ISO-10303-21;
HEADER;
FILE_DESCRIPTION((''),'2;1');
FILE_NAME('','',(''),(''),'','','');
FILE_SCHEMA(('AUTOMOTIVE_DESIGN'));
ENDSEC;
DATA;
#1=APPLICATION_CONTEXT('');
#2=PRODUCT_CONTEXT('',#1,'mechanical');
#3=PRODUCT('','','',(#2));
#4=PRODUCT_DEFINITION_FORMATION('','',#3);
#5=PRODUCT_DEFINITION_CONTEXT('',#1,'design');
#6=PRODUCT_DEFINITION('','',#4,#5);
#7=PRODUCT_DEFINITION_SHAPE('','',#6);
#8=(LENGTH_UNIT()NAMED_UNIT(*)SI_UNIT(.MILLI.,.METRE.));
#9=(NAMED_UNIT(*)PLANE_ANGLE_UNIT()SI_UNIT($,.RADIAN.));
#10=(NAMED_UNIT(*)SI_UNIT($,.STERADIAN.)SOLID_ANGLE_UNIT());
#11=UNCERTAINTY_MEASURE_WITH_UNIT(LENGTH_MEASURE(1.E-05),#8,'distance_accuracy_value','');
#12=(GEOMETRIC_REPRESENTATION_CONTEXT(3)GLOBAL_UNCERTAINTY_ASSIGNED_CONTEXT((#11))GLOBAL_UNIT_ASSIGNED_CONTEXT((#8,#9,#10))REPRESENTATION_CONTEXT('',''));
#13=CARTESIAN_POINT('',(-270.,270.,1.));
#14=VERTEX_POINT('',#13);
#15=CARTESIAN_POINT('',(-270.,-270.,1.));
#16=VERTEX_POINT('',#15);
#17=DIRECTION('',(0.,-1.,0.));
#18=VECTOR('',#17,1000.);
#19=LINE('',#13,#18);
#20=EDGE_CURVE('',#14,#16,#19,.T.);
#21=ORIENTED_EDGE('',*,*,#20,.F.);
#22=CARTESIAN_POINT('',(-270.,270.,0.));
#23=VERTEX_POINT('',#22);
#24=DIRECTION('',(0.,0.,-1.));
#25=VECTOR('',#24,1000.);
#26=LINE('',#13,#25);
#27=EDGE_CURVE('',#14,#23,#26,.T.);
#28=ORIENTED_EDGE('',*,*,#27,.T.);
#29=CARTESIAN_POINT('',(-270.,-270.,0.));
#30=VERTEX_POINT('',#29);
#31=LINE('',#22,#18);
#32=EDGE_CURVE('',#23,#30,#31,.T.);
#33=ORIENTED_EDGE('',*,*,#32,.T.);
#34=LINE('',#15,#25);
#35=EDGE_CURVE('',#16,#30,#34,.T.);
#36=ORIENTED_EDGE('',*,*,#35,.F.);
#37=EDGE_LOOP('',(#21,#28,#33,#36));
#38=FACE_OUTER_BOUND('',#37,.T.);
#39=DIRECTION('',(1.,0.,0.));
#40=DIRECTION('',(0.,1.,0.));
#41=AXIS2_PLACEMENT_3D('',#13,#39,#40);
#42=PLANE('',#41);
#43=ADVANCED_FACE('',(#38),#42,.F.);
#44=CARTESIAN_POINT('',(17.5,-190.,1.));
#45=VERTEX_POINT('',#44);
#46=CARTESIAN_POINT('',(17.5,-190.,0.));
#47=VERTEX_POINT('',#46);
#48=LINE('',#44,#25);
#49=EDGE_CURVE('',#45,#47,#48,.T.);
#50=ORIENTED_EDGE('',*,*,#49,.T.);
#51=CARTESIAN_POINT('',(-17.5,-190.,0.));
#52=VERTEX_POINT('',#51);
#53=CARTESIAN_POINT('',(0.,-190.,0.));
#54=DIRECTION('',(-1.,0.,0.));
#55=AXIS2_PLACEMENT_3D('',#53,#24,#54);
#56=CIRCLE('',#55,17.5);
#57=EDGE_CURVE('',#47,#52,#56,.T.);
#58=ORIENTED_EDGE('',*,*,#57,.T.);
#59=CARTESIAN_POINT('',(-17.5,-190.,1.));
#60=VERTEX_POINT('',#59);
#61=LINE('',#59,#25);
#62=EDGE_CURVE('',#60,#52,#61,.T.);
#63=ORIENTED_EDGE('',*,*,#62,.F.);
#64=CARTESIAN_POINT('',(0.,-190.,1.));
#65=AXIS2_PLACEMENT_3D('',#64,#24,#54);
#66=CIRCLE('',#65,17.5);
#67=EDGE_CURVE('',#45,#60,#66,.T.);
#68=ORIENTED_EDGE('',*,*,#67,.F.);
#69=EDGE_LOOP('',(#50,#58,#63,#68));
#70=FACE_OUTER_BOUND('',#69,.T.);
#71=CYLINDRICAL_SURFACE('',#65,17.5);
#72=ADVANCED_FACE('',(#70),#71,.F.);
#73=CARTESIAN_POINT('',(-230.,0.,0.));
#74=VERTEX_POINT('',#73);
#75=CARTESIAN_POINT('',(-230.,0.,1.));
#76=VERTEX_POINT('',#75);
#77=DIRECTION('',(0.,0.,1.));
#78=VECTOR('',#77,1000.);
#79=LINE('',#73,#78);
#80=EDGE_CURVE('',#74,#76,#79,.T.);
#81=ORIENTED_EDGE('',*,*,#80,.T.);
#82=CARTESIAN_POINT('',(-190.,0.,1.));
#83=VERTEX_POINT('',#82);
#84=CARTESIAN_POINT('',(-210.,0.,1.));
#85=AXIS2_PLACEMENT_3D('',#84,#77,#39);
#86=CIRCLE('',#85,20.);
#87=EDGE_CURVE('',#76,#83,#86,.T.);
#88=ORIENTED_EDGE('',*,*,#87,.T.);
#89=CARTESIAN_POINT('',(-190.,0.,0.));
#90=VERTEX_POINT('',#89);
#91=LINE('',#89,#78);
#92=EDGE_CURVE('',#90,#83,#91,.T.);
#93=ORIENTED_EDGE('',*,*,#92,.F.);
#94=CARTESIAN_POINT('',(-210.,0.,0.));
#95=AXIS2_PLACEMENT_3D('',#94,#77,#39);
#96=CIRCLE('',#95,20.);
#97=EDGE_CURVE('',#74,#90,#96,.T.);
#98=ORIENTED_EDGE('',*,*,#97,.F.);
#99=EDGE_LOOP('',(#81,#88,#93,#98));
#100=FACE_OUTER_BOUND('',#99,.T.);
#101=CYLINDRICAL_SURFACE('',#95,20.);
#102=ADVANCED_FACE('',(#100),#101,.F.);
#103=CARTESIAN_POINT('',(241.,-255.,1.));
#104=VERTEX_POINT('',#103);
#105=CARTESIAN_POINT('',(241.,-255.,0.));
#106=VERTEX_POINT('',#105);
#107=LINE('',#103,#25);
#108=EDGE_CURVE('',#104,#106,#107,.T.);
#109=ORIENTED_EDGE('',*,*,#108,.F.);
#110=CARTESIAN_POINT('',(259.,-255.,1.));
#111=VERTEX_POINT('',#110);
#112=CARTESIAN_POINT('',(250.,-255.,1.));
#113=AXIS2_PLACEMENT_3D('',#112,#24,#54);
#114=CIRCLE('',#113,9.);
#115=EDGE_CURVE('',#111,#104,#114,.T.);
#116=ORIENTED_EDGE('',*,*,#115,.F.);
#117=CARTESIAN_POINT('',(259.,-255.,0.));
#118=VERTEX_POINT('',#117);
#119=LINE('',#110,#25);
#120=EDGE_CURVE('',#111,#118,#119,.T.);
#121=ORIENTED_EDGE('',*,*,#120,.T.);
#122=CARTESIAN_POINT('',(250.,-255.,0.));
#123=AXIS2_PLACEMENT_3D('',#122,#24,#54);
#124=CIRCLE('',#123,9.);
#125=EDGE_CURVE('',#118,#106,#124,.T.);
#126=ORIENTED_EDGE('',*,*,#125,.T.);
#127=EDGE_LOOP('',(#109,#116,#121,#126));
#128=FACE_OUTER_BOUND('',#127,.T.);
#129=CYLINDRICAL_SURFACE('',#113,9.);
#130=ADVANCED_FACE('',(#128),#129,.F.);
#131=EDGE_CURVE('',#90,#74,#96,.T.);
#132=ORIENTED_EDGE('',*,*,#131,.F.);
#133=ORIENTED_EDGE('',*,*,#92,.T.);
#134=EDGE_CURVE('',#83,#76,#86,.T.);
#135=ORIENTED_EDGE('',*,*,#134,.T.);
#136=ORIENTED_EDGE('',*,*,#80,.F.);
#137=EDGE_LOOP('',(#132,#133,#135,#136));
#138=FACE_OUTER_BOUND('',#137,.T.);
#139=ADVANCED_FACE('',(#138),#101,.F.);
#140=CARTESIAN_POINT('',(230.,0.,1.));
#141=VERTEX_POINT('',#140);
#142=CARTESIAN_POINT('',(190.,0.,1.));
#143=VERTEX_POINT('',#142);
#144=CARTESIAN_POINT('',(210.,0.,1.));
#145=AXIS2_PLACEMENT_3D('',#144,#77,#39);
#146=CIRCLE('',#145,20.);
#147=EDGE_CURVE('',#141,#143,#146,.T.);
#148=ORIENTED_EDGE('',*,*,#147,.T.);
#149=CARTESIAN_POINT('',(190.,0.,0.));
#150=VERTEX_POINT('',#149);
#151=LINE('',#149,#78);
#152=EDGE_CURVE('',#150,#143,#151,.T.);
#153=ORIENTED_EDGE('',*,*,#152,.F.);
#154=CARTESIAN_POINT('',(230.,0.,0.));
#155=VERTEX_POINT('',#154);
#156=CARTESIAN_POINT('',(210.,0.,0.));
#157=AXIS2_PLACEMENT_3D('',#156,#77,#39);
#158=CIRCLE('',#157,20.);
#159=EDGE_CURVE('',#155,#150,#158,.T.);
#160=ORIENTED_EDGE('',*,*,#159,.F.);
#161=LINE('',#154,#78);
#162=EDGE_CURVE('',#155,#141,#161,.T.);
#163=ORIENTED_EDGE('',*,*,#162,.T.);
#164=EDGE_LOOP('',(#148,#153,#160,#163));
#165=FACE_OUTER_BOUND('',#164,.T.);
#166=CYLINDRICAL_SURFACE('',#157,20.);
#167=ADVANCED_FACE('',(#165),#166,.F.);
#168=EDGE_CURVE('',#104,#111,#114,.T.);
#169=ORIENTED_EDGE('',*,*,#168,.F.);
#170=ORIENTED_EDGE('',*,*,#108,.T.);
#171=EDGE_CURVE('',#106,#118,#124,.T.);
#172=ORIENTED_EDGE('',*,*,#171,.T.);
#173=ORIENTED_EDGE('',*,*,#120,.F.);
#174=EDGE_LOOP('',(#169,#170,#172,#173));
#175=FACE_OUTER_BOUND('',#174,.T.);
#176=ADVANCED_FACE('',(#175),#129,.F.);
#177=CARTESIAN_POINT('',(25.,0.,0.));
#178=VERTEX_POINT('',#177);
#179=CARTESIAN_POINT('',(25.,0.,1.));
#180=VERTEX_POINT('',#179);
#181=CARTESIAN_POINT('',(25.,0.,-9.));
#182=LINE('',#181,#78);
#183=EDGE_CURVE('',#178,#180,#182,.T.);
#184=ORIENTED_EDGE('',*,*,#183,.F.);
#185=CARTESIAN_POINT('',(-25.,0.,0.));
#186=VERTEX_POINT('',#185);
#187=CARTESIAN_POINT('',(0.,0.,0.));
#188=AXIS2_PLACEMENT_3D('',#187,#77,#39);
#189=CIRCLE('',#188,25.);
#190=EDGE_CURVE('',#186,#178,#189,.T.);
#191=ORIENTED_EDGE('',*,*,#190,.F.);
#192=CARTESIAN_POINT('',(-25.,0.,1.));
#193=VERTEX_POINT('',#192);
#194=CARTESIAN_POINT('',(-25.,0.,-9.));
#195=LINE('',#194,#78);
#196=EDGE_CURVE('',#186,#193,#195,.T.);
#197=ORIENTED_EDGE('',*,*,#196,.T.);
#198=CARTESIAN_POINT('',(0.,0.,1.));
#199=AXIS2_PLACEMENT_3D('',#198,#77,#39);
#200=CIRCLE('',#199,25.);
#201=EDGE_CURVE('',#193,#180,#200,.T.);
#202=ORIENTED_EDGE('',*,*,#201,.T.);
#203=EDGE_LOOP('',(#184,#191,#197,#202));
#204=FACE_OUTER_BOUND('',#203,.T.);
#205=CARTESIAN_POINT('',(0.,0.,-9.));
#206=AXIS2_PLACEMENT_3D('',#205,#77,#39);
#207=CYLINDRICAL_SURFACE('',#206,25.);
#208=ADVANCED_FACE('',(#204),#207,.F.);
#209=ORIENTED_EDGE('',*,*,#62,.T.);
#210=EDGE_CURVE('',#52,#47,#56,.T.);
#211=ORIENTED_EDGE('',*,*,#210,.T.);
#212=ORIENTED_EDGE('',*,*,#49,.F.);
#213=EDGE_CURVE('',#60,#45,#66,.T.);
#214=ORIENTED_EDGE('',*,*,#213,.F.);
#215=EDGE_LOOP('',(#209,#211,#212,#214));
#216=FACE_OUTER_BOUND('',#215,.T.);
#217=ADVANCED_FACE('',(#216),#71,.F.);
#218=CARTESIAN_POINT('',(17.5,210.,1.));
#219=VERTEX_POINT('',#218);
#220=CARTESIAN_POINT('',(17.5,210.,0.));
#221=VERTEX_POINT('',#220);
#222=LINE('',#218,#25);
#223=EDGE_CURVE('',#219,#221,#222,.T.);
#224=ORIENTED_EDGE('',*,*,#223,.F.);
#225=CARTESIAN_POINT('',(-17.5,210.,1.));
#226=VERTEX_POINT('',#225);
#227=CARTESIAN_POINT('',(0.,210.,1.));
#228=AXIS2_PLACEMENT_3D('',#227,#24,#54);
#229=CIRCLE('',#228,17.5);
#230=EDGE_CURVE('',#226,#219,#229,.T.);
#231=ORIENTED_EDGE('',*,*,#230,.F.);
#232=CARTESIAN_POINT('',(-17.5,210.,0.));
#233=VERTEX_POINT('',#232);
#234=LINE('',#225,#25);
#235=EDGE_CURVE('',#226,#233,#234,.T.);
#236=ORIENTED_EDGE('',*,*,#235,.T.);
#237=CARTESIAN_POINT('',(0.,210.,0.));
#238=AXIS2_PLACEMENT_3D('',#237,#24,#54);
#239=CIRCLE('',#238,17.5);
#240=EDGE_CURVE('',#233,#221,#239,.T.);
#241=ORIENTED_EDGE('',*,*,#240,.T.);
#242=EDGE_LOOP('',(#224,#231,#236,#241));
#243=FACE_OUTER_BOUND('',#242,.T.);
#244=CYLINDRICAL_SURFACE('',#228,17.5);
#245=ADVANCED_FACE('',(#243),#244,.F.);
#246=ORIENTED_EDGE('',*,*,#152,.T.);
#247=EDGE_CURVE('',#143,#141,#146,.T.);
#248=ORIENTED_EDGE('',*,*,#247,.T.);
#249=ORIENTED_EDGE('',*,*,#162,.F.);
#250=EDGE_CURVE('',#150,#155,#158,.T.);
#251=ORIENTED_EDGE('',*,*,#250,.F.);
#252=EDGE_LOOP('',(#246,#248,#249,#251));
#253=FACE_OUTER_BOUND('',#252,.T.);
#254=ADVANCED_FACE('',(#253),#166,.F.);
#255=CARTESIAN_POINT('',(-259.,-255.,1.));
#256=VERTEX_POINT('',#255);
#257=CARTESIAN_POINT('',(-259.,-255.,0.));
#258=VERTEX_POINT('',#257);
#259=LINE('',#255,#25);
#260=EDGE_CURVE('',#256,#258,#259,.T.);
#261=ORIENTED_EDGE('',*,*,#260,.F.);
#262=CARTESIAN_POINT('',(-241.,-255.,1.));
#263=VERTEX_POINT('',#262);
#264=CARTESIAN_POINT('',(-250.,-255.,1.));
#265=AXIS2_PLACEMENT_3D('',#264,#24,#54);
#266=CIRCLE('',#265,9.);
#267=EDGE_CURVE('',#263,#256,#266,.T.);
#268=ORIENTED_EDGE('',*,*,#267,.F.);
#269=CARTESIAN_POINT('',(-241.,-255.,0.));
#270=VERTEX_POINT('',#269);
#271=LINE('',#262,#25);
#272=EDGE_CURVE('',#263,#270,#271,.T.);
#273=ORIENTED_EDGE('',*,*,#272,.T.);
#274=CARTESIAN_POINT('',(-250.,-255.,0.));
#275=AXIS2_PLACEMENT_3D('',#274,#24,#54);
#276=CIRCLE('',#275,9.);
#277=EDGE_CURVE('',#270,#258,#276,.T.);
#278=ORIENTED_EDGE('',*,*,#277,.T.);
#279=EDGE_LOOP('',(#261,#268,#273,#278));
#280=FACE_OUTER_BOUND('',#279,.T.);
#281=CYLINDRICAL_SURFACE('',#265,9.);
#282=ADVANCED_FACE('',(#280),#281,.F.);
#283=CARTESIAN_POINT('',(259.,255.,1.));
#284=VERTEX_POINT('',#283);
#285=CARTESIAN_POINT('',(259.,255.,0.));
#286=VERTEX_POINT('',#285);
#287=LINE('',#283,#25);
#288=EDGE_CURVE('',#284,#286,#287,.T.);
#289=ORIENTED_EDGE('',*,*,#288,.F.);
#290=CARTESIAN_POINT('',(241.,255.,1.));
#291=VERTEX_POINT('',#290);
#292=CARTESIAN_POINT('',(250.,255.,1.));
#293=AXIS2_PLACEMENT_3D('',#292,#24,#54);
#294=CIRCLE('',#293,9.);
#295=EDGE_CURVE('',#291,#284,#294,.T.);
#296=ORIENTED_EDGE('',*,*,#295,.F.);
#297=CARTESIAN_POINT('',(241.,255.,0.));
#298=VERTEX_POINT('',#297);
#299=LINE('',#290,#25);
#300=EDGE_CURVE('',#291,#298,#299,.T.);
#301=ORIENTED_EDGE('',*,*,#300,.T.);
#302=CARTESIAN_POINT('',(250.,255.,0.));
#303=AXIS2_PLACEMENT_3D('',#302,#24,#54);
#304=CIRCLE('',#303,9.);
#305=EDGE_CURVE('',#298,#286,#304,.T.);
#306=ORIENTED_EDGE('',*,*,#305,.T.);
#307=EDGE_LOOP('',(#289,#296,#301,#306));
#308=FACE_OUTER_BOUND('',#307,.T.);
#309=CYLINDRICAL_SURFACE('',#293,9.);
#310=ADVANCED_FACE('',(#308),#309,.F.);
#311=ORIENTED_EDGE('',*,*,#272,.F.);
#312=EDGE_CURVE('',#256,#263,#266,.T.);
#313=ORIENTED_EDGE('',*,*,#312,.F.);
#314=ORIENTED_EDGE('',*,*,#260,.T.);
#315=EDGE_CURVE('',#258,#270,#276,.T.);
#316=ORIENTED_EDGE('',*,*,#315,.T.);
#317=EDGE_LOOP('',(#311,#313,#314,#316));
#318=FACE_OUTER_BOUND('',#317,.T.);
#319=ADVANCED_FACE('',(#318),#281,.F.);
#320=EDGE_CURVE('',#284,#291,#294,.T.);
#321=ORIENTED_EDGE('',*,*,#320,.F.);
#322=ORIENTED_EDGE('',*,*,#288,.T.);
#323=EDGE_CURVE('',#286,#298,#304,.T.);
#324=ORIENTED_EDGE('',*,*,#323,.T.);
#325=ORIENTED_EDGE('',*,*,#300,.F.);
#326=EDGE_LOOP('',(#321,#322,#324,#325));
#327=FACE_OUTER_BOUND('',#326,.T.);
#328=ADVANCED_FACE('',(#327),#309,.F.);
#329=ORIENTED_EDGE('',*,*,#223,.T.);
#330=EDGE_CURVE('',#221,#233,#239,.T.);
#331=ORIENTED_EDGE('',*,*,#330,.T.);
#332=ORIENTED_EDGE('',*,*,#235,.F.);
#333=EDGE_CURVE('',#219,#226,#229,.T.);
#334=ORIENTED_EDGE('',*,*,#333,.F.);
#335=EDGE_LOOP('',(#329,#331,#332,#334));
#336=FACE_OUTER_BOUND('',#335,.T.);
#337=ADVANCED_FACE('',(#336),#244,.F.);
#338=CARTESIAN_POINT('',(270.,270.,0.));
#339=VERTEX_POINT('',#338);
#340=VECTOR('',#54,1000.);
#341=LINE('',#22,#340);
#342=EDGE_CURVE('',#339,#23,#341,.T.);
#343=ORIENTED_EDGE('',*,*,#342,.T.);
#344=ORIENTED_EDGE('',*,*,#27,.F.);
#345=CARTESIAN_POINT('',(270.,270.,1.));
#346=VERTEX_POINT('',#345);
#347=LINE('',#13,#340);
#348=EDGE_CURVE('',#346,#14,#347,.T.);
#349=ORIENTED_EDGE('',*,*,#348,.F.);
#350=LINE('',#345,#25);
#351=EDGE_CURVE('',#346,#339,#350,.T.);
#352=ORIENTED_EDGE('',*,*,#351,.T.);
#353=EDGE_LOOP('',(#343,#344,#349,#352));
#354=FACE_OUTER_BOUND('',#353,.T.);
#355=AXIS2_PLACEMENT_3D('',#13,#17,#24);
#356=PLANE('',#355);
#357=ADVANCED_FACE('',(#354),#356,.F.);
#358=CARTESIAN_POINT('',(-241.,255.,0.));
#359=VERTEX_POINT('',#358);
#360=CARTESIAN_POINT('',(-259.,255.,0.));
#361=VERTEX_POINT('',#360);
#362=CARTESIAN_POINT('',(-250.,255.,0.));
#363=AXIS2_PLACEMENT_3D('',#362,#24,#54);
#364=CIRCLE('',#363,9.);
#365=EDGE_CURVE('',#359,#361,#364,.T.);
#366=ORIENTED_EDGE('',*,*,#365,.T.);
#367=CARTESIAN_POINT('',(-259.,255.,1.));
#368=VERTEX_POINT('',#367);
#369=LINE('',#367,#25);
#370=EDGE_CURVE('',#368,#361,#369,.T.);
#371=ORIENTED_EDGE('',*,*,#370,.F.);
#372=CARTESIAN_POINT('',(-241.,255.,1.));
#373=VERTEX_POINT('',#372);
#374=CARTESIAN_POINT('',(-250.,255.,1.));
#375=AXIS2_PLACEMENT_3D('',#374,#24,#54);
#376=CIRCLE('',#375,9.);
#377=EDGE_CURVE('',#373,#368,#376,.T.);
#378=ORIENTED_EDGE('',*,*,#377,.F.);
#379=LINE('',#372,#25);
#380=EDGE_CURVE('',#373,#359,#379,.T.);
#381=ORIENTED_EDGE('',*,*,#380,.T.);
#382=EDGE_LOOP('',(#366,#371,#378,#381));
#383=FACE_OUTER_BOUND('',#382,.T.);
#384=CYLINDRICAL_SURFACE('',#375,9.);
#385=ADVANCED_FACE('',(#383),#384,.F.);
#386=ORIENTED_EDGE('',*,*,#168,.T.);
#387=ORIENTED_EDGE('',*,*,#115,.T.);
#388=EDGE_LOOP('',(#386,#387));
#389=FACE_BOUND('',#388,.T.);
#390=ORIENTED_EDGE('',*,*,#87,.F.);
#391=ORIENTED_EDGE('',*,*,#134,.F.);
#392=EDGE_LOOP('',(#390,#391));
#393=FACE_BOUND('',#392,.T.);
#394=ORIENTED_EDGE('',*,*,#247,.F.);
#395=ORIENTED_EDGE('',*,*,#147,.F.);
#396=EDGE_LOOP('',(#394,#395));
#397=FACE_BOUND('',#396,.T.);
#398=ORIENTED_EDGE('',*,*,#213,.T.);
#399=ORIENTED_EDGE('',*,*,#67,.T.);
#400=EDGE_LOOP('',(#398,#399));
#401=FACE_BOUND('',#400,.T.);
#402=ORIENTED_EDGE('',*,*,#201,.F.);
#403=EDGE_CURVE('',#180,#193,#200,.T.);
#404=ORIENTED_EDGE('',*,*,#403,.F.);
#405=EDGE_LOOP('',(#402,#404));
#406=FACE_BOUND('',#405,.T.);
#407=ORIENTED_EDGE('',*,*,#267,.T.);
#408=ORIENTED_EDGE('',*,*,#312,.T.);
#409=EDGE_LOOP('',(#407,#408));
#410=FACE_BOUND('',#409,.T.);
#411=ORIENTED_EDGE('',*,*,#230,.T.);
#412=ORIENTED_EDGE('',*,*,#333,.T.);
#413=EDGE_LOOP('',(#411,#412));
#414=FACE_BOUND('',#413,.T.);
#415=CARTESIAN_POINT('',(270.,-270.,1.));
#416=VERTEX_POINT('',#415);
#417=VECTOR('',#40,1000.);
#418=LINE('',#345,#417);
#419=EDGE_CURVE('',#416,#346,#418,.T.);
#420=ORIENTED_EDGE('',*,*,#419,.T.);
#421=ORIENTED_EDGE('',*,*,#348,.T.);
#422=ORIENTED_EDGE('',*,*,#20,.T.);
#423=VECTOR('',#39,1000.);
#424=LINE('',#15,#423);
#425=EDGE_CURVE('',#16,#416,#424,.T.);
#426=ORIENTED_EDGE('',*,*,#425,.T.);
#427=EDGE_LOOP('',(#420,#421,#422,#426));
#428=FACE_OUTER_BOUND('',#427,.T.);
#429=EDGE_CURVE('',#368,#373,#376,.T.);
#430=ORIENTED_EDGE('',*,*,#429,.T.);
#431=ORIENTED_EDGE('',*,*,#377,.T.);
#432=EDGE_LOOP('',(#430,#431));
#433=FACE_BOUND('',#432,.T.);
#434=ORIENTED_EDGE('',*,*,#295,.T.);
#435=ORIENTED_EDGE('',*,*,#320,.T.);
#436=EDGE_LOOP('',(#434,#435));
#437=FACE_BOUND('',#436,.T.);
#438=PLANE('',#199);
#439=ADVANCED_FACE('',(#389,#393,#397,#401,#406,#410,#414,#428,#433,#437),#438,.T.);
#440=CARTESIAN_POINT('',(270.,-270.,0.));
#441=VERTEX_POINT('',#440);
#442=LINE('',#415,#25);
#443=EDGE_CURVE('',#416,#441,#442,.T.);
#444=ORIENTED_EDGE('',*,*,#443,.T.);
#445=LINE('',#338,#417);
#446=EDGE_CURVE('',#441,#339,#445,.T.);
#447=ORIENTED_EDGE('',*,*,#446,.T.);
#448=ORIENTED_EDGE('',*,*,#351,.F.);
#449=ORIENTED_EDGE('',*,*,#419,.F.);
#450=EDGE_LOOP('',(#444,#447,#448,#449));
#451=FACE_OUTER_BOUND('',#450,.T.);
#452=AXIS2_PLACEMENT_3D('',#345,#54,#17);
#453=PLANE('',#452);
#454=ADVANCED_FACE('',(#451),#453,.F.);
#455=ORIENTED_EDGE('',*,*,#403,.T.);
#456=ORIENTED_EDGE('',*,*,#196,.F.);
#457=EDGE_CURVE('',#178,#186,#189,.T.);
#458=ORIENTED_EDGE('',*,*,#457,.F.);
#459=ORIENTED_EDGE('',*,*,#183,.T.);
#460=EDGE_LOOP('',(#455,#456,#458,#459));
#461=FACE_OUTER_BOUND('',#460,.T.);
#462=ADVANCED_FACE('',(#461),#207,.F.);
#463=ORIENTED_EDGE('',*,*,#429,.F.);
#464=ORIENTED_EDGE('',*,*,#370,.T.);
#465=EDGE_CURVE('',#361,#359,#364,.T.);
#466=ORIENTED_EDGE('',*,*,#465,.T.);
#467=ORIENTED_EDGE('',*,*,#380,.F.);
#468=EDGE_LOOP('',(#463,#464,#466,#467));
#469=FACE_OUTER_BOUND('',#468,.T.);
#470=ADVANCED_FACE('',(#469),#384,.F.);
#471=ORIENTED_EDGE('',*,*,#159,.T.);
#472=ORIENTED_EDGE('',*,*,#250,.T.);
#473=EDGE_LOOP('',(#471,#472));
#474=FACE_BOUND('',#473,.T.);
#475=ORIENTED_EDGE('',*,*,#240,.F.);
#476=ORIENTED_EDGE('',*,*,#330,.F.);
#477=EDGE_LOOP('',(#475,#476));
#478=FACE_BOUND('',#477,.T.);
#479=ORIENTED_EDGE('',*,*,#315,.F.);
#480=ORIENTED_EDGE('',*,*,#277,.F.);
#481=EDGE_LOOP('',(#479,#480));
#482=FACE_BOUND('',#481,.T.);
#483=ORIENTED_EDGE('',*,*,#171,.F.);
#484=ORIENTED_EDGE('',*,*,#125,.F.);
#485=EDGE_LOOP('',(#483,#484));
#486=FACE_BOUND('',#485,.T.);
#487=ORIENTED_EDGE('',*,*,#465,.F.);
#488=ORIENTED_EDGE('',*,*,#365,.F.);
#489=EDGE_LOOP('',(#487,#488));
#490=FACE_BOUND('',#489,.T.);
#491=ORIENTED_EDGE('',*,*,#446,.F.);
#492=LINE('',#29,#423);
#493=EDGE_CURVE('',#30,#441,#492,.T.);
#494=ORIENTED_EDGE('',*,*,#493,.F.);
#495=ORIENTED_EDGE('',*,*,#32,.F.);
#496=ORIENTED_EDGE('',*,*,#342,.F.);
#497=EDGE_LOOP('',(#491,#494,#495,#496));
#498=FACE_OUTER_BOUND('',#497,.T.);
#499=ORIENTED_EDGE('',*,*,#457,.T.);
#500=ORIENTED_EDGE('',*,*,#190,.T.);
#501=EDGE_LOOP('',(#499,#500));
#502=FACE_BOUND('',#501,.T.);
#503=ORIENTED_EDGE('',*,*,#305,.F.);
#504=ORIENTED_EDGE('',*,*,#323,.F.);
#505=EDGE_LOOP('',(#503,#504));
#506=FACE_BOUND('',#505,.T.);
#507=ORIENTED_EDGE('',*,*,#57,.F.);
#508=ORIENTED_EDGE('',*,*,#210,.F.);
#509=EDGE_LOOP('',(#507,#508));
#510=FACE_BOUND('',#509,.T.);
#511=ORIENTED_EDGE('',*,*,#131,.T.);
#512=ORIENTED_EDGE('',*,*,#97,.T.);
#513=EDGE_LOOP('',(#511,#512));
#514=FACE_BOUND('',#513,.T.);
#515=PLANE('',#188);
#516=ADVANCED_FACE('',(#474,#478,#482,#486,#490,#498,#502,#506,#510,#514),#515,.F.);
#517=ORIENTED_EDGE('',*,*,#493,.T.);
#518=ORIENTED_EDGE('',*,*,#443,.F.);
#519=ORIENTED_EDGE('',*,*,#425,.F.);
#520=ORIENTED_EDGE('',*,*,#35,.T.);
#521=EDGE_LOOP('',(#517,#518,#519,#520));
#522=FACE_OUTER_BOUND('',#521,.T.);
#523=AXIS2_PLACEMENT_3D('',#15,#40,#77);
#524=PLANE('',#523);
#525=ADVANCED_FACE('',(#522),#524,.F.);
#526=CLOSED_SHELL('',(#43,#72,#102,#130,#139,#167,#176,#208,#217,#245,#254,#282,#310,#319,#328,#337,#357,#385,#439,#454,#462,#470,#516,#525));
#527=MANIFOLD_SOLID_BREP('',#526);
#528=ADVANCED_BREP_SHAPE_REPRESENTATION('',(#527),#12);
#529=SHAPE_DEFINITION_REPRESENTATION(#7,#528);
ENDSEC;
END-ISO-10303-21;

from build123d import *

# Parameters (mm, degrees)
SKETCH_1_W          = 540
SKETCH_1_H          = 540
EXTRUDE_1_DEPTH     = 1
SKETCH_2_R          = 9
CUT_EXTRUDE_1_DEPTH = 382.838971295
SKETCH_3_R          = 20
CUT_EXTRUDE_2_DEPTH = 382.838971295
SKETCH_4_R          = 25
CUT_EXTRUDE_3_DEPTH = 10
SKETCH_5_R          = 17.5
CUT_EXTRUDE_4_DEPTH = 382.838971295


with BuildPart() as part:
    # 草图1 → 凸台-拉伸1 (new body)
    with BuildSketch(Plane.XY):
        Rectangle(SKETCH_1_W, SKETCH_1_H)
    extrude(amount=EXTRUDE_1_DEPTH)

    # 草图2 → 切除-拉伸1 (cut, through all)
    with BuildSketch(Plane(origin=(0, 0, 0), x_dir=(-1, 0, 0), z_dir=(0, 0, -1))):
        with Locations((250, -255)):
            Circle(SKETCH_2_R)
        with Locations((-250, -255)):
            Circle(SKETCH_2_R)
        with Locations((250, 255)):
            Circle(SKETCH_2_R)
        with Locations((-250, 255)):
            Circle(SKETCH_2_R)
    extrude(amount=-CUT_EXTRUDE_1_DEPTH, mode=Mode.SUBTRACT)

    # 草图3 → 切除-拉伸2 (cut, through all)
    with BuildSketch(Plane.XY.offset(1)):
        with Locations((-210, 0)):
            Circle(SKETCH_3_R)
        with Locations((210, 0)):
            Circle(SKETCH_3_R)
    extrude(amount=-CUT_EXTRUDE_2_DEPTH, mode=Mode.SUBTRACT)

    # 草图4 → 切除-拉伸3 (cut)
    with BuildSketch(Plane.XY.offset(1)):
        Circle(SKETCH_4_R)
    extrude(amount=-CUT_EXTRUDE_3_DEPTH, mode=Mode.SUBTRACT)

    # 草图5 → 切除-拉伸4 (cut, through all)
    with BuildSketch(Plane(origin=(0, 0, 0), x_dir=(-1, 0, 0), z_dir=(0, 0, -1))):
        with Locations((0, -190)):
            Circle(SKETCH_5_R)
        with Locations((0, 210)):
            Circle(SKETCH_5_R)
    extrude(amount=-CUT_EXTRUDE_4_DEPTH, mode=Mode.SUBTRACT)


solid = part.part
